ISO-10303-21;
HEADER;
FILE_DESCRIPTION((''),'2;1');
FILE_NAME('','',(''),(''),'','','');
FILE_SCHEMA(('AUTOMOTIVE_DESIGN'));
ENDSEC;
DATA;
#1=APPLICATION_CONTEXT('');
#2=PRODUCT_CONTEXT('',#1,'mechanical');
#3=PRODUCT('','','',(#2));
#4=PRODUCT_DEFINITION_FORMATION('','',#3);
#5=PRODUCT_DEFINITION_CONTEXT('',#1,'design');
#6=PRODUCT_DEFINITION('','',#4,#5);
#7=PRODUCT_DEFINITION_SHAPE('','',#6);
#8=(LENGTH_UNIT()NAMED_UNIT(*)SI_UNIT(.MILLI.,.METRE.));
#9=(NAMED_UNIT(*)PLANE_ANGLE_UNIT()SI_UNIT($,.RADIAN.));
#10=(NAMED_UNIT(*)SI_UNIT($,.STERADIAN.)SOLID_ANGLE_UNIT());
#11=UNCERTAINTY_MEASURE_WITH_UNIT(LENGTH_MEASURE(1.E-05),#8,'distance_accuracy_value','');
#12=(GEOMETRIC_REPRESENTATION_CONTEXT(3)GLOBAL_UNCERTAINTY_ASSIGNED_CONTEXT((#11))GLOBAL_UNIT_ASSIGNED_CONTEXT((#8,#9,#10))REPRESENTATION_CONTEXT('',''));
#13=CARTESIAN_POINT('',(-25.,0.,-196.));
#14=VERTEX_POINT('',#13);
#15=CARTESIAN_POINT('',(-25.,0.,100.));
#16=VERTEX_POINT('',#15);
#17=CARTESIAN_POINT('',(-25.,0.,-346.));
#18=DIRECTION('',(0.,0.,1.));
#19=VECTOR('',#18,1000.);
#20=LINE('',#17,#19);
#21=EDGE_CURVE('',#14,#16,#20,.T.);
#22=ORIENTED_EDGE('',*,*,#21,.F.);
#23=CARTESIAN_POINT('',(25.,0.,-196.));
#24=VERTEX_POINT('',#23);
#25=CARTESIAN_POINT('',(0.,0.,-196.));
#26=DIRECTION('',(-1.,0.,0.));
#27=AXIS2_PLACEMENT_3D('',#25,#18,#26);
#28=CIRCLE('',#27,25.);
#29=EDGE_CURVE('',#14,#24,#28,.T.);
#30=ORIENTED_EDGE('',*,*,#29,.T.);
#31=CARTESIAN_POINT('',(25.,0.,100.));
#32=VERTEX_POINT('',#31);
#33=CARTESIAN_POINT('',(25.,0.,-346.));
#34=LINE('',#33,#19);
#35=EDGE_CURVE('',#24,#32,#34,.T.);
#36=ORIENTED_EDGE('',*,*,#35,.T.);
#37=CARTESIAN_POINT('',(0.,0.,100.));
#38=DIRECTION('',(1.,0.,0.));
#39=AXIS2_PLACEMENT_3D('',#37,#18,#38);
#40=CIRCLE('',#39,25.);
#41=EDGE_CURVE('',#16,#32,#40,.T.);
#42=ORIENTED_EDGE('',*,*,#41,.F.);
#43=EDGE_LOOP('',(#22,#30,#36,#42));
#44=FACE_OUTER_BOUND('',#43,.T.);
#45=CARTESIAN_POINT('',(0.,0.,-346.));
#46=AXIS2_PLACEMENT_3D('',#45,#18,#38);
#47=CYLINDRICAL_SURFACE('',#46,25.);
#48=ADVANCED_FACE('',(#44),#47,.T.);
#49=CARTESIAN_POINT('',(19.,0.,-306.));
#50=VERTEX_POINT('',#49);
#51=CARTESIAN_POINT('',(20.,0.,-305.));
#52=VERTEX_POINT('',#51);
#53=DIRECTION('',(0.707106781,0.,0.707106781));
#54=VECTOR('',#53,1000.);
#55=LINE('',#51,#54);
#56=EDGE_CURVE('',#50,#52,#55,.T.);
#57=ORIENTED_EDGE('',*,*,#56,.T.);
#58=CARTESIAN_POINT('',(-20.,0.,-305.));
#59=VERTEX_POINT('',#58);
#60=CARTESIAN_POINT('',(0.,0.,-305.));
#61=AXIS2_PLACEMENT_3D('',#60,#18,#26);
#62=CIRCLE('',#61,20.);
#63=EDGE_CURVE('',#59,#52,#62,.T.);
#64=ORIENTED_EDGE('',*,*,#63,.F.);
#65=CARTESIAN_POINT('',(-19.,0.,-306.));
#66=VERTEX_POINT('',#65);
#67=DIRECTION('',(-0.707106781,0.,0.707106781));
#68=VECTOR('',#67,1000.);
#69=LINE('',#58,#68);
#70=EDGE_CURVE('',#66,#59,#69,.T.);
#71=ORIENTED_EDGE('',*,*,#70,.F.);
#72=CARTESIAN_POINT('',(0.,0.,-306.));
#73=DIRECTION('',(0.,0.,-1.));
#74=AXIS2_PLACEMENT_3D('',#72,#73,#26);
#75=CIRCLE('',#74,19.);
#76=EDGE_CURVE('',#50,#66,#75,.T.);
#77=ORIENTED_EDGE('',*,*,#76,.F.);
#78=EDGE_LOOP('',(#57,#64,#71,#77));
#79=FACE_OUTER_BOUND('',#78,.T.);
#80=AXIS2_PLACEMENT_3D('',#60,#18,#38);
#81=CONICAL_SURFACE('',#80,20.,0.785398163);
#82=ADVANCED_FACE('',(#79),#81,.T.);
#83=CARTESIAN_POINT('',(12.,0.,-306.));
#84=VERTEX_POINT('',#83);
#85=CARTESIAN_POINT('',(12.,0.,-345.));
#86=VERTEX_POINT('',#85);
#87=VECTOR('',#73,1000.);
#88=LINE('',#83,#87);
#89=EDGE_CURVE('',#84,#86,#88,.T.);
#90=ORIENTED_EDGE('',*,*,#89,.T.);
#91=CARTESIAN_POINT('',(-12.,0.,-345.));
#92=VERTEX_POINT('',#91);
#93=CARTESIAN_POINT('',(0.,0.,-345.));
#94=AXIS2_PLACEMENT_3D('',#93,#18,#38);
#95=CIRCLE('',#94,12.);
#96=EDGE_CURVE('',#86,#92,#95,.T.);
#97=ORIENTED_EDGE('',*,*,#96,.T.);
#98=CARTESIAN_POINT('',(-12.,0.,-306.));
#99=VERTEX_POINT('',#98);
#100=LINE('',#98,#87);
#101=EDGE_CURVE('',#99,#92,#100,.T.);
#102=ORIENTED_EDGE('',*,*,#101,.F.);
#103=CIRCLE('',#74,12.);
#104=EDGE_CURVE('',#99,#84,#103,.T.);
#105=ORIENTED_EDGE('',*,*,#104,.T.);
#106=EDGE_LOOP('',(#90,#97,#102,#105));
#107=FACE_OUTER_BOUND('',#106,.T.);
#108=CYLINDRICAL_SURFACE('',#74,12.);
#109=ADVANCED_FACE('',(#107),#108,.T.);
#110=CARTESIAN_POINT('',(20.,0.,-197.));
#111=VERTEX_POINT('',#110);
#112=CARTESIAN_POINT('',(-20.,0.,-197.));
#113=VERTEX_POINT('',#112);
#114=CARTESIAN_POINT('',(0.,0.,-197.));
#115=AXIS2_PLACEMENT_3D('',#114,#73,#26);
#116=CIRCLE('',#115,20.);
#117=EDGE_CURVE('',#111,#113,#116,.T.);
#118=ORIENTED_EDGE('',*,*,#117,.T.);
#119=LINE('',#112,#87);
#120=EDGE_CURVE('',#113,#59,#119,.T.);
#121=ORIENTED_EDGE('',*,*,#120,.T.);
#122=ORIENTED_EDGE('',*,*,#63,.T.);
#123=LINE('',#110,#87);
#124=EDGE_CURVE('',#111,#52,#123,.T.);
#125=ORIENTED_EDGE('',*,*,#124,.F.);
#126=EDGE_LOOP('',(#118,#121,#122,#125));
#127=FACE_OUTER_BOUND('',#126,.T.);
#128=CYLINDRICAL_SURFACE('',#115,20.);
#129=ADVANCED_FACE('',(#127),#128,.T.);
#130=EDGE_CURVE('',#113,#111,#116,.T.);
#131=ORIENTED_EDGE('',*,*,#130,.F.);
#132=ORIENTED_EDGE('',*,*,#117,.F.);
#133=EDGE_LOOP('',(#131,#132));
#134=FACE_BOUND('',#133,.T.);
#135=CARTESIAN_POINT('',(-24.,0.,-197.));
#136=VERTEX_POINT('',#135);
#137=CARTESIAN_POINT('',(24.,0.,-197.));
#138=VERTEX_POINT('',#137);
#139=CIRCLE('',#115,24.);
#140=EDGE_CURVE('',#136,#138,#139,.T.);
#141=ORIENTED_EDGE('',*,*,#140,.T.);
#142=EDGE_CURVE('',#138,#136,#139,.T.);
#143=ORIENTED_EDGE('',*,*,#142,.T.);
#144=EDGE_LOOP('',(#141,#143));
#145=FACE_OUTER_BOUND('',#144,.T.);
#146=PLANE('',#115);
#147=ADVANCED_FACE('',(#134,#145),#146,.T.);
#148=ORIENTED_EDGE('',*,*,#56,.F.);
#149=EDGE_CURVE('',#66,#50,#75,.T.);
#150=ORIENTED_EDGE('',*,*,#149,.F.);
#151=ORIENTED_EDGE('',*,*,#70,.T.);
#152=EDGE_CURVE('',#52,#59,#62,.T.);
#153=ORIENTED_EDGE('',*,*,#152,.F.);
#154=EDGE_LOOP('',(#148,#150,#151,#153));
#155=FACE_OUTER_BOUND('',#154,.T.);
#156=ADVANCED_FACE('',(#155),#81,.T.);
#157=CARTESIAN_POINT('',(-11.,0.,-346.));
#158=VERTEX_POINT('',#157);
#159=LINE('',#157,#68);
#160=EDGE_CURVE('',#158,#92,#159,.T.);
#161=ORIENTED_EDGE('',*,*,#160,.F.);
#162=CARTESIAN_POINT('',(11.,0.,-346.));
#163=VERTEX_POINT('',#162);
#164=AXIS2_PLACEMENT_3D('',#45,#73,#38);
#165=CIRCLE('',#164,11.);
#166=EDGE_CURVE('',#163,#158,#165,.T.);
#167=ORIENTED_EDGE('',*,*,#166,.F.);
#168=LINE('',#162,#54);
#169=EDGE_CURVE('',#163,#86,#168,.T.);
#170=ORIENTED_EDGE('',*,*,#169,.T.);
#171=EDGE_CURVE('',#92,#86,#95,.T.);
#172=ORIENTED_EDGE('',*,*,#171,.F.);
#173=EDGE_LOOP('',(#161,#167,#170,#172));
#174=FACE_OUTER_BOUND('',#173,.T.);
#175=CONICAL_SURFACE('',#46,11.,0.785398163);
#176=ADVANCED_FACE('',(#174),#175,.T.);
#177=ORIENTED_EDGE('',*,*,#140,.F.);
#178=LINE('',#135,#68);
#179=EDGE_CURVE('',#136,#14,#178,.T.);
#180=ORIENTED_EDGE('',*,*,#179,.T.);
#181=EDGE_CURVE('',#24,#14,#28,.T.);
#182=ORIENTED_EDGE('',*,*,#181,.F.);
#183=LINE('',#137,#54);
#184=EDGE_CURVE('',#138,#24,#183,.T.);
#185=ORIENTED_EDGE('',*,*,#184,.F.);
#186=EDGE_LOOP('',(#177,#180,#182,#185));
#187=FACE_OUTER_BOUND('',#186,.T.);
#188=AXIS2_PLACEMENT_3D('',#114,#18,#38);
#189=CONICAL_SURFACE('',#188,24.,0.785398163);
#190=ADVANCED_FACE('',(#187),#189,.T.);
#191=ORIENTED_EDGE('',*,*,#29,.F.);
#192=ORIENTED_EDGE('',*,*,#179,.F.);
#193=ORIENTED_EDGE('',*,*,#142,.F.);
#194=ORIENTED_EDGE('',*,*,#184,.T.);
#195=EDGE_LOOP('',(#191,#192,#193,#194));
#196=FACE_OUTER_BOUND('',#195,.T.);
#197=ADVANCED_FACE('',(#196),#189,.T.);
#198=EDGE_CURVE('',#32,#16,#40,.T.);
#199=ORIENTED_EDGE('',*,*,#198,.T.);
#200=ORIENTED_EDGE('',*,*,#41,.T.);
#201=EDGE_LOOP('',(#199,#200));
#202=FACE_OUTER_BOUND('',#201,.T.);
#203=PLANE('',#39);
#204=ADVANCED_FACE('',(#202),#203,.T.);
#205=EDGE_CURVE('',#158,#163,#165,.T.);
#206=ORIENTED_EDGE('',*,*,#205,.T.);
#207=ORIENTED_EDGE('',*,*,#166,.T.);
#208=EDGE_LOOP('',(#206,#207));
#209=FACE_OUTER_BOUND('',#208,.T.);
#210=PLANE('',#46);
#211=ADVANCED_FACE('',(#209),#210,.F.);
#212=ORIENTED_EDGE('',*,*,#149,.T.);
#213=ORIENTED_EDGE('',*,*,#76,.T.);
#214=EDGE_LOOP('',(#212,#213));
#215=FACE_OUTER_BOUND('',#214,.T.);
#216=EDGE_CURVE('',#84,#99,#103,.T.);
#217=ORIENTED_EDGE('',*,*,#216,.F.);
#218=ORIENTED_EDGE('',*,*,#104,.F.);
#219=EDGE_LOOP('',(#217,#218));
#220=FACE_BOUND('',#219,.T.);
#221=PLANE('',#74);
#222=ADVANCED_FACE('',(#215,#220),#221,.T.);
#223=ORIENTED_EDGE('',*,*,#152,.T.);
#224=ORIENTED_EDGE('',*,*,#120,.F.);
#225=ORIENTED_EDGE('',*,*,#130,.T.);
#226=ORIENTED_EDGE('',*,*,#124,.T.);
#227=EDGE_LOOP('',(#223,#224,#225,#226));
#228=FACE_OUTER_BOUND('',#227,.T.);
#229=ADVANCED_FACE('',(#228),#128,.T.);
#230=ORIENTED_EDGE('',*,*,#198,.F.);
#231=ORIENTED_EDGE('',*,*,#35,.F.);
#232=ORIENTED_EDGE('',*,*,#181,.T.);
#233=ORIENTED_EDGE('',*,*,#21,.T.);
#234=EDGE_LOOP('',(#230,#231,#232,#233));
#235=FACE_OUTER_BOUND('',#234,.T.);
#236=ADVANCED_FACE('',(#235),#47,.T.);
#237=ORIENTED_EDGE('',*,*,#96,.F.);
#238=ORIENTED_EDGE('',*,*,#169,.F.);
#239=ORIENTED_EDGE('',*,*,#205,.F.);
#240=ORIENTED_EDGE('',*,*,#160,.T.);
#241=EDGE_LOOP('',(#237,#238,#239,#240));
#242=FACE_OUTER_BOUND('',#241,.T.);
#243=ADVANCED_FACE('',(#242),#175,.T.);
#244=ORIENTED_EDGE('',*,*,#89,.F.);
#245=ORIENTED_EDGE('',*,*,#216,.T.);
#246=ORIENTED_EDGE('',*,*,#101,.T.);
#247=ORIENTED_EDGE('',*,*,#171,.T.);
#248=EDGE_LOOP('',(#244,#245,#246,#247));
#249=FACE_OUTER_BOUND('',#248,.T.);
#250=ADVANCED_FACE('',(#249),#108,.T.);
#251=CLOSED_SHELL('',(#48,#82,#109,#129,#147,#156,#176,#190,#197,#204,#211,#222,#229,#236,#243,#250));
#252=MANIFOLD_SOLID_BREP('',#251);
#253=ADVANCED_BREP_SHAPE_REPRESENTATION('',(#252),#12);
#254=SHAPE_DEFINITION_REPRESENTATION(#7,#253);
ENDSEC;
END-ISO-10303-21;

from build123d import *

# Parameters (mm, degrees)
EXTRUDE_1_DEPTH      = 100
EXTRUDE_1_DEPTH_BACK = 346
SKETCH_1_R           = 25
SKETCH_2_R           = 25
SKETCH_2_R_2         = 20
CUT_EXTRUDE_1_DEPTH  = 109
SKETCH_3_R           = 25
SKETCH_3_R_2         = 12
CUT_EXTRUDE_2_DEPTH  = 40
CHAMFER_1_SIZE       = 1


with BuildPart() as part:
    # 草图1 → 凸台-拉伸1 (new, two sides: drawn at the far end of the back side and taken through both)
    with BuildSketch(Plane.XY.offset(-EXTRUDE_1_DEPTH_BACK)):
        Circle(SKETCH_1_R)
    extrude(amount=EXTRUDE_1_DEPTH + EXTRUDE_1_DEPTH_BACK)

    # 草图2 → 切除-拉伸1 (cut)
    with BuildSketch(Plane(origin=(0, 0, -306), x_dir=(-1, 0, 0), z_dir=(0, 0, -1))):
        with Locations(Location((0, 0, 0), (0, 0, 180))):
            Circle(SKETCH_2_R)
        Circle(SKETCH_2_R_2, mode=Mode.SUBTRACT)
    extrude(amount=-CUT_EXTRUDE_1_DEPTH, mode=Mode.SUBTRACT)

    # 草图3 → 切除-拉伸2 (cut)
    with BuildSketch(Plane(origin=(0, 0, -346), x_dir=(-1, 0, 0), z_dir=(0, 0, -1))):
        with Locations(Location((0, 0, 0), (0, 0, 180))):
            Circle(SKETCH_3_R)
        Circle(SKETCH_3_R_2, mode=Mode.SUBTRACT)
    extrude(amount=-CUT_EXTRUDE_2_DEPTH, mode=Mode.SUBTRACT)

    # 倒角1
    chamfer_1_edges = [part.edges().sort_by_distance(p)[0] for p in [
        (20, 0, -306),
        (12, 0, -346),
        (-25, 0, -197),
    ]]
    chamfer(chamfer_1_edges, length=CHAMFER_1_SIZE)


solid = part.part
